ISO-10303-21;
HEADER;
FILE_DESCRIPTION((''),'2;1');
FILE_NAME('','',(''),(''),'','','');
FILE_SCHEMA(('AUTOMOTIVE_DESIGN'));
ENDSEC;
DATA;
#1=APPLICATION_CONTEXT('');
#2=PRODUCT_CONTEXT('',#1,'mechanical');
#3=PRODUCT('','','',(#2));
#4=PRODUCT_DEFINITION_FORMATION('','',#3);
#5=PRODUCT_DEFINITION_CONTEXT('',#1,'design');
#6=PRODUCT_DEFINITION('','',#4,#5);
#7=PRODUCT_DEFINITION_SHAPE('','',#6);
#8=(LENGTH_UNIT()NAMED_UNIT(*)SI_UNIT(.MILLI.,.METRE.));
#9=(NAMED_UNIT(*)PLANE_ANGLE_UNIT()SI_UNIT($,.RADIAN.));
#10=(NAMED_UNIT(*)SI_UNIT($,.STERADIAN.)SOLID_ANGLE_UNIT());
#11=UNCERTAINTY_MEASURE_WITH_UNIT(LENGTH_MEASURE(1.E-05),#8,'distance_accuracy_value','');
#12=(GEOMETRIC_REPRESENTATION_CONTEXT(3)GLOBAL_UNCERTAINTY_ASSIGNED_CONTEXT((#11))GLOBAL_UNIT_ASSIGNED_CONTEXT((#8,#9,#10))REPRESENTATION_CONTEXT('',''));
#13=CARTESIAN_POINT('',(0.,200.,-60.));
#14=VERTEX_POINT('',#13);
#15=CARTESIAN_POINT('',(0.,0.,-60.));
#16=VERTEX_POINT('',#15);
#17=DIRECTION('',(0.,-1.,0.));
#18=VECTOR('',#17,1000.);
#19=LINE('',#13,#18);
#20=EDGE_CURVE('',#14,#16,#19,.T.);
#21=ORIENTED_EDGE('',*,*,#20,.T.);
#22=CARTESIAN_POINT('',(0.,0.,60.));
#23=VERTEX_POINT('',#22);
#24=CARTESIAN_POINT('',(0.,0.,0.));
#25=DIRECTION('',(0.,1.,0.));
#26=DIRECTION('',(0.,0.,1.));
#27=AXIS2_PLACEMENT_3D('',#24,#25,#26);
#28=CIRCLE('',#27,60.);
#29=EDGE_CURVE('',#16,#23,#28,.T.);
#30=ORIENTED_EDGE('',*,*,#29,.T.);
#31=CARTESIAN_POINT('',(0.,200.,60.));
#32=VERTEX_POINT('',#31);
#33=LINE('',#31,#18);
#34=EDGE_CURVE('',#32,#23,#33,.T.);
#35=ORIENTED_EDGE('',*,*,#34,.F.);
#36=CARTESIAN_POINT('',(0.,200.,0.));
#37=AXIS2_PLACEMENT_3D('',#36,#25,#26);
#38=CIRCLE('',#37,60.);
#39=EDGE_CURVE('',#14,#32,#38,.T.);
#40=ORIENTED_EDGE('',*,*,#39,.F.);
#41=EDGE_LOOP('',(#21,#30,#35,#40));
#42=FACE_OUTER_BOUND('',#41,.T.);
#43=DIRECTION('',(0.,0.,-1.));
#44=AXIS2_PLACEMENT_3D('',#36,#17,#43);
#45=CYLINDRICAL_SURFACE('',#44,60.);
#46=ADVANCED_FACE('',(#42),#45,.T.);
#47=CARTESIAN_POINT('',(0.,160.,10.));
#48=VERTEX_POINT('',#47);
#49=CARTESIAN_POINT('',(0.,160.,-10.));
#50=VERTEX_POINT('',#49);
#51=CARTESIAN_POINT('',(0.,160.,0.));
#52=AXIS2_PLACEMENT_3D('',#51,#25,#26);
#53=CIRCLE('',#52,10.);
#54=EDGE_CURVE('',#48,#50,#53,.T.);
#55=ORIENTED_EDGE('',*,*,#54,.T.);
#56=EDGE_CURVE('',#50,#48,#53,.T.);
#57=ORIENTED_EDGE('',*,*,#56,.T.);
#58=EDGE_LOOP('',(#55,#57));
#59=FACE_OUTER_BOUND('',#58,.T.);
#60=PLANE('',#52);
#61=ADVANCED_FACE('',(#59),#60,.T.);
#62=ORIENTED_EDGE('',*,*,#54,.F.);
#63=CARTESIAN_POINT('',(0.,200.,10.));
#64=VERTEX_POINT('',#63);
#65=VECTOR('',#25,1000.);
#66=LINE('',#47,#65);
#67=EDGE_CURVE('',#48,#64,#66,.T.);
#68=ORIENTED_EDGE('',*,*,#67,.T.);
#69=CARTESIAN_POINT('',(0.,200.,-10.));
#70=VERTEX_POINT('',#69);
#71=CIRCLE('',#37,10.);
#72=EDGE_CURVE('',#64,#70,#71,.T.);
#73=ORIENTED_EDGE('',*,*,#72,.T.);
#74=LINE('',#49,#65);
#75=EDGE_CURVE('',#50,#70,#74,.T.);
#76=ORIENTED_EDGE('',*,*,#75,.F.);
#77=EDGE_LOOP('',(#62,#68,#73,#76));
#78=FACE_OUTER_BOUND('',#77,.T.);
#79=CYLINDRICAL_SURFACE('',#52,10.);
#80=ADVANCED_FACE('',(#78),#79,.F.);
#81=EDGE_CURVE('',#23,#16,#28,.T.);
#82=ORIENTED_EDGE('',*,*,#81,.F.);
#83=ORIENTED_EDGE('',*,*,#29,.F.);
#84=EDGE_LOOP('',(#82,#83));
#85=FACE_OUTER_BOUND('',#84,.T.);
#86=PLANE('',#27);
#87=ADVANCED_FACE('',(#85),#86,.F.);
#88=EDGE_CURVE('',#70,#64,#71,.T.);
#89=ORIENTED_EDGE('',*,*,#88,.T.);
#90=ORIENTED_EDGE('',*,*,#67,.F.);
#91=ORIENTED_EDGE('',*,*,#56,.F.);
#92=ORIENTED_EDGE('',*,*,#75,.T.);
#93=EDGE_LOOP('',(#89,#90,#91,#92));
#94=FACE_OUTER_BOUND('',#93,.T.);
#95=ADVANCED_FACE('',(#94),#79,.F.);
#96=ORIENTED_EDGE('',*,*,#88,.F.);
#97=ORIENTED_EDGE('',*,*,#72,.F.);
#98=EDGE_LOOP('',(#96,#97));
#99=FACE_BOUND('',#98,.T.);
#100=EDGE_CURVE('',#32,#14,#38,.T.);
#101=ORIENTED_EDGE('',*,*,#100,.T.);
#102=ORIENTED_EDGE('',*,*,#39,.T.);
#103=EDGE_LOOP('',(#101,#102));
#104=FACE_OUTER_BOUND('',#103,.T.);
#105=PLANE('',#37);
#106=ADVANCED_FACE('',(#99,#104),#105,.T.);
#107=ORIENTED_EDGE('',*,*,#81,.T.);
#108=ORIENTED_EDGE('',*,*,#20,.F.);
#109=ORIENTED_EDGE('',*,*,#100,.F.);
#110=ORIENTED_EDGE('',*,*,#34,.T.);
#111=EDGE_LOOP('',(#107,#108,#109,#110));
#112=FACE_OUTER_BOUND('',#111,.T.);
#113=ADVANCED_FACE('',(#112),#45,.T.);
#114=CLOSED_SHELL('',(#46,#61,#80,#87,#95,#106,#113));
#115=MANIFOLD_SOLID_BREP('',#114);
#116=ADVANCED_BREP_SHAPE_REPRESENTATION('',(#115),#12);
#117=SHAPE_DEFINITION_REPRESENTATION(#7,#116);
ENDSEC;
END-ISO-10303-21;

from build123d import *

# Parameters (mm, degrees)
SKETCH1_R           = 60
BOSS_EXTRUDE2_DEPTH = 200
SKETCH3_R           = 10
CUT_EXTRUDE2_DEPTH  = 40


with BuildPart() as part:
    # Sketch1 → Boss-Extrude2 (new body)
    with BuildSketch(Plane(origin=(0, 0, 0), x_dir=(1, 0, 0), z_dir=(0, 1, 0))):
        with Locations(Location((0, 0, 0), (0, 0, 270))):
            Circle(SKETCH1_R)
    extrude(amount=BOSS_EXTRUDE2_DEPTH)

    # Sketch3 → Cut-Extrude2 (cut)
    with BuildSketch(Plane(origin=(0, 200, 0), x_dir=(1, 0, 0), z_dir=(0, 1, 0))):
        with Locations(Location((0, 0, 0), (0, 0, 270))):
            Circle(SKETCH3_R)
    extrude(amount=-CUT_EXTRUDE2_DEPTH, mode=Mode.SUBTRACT)


solid = part.part
